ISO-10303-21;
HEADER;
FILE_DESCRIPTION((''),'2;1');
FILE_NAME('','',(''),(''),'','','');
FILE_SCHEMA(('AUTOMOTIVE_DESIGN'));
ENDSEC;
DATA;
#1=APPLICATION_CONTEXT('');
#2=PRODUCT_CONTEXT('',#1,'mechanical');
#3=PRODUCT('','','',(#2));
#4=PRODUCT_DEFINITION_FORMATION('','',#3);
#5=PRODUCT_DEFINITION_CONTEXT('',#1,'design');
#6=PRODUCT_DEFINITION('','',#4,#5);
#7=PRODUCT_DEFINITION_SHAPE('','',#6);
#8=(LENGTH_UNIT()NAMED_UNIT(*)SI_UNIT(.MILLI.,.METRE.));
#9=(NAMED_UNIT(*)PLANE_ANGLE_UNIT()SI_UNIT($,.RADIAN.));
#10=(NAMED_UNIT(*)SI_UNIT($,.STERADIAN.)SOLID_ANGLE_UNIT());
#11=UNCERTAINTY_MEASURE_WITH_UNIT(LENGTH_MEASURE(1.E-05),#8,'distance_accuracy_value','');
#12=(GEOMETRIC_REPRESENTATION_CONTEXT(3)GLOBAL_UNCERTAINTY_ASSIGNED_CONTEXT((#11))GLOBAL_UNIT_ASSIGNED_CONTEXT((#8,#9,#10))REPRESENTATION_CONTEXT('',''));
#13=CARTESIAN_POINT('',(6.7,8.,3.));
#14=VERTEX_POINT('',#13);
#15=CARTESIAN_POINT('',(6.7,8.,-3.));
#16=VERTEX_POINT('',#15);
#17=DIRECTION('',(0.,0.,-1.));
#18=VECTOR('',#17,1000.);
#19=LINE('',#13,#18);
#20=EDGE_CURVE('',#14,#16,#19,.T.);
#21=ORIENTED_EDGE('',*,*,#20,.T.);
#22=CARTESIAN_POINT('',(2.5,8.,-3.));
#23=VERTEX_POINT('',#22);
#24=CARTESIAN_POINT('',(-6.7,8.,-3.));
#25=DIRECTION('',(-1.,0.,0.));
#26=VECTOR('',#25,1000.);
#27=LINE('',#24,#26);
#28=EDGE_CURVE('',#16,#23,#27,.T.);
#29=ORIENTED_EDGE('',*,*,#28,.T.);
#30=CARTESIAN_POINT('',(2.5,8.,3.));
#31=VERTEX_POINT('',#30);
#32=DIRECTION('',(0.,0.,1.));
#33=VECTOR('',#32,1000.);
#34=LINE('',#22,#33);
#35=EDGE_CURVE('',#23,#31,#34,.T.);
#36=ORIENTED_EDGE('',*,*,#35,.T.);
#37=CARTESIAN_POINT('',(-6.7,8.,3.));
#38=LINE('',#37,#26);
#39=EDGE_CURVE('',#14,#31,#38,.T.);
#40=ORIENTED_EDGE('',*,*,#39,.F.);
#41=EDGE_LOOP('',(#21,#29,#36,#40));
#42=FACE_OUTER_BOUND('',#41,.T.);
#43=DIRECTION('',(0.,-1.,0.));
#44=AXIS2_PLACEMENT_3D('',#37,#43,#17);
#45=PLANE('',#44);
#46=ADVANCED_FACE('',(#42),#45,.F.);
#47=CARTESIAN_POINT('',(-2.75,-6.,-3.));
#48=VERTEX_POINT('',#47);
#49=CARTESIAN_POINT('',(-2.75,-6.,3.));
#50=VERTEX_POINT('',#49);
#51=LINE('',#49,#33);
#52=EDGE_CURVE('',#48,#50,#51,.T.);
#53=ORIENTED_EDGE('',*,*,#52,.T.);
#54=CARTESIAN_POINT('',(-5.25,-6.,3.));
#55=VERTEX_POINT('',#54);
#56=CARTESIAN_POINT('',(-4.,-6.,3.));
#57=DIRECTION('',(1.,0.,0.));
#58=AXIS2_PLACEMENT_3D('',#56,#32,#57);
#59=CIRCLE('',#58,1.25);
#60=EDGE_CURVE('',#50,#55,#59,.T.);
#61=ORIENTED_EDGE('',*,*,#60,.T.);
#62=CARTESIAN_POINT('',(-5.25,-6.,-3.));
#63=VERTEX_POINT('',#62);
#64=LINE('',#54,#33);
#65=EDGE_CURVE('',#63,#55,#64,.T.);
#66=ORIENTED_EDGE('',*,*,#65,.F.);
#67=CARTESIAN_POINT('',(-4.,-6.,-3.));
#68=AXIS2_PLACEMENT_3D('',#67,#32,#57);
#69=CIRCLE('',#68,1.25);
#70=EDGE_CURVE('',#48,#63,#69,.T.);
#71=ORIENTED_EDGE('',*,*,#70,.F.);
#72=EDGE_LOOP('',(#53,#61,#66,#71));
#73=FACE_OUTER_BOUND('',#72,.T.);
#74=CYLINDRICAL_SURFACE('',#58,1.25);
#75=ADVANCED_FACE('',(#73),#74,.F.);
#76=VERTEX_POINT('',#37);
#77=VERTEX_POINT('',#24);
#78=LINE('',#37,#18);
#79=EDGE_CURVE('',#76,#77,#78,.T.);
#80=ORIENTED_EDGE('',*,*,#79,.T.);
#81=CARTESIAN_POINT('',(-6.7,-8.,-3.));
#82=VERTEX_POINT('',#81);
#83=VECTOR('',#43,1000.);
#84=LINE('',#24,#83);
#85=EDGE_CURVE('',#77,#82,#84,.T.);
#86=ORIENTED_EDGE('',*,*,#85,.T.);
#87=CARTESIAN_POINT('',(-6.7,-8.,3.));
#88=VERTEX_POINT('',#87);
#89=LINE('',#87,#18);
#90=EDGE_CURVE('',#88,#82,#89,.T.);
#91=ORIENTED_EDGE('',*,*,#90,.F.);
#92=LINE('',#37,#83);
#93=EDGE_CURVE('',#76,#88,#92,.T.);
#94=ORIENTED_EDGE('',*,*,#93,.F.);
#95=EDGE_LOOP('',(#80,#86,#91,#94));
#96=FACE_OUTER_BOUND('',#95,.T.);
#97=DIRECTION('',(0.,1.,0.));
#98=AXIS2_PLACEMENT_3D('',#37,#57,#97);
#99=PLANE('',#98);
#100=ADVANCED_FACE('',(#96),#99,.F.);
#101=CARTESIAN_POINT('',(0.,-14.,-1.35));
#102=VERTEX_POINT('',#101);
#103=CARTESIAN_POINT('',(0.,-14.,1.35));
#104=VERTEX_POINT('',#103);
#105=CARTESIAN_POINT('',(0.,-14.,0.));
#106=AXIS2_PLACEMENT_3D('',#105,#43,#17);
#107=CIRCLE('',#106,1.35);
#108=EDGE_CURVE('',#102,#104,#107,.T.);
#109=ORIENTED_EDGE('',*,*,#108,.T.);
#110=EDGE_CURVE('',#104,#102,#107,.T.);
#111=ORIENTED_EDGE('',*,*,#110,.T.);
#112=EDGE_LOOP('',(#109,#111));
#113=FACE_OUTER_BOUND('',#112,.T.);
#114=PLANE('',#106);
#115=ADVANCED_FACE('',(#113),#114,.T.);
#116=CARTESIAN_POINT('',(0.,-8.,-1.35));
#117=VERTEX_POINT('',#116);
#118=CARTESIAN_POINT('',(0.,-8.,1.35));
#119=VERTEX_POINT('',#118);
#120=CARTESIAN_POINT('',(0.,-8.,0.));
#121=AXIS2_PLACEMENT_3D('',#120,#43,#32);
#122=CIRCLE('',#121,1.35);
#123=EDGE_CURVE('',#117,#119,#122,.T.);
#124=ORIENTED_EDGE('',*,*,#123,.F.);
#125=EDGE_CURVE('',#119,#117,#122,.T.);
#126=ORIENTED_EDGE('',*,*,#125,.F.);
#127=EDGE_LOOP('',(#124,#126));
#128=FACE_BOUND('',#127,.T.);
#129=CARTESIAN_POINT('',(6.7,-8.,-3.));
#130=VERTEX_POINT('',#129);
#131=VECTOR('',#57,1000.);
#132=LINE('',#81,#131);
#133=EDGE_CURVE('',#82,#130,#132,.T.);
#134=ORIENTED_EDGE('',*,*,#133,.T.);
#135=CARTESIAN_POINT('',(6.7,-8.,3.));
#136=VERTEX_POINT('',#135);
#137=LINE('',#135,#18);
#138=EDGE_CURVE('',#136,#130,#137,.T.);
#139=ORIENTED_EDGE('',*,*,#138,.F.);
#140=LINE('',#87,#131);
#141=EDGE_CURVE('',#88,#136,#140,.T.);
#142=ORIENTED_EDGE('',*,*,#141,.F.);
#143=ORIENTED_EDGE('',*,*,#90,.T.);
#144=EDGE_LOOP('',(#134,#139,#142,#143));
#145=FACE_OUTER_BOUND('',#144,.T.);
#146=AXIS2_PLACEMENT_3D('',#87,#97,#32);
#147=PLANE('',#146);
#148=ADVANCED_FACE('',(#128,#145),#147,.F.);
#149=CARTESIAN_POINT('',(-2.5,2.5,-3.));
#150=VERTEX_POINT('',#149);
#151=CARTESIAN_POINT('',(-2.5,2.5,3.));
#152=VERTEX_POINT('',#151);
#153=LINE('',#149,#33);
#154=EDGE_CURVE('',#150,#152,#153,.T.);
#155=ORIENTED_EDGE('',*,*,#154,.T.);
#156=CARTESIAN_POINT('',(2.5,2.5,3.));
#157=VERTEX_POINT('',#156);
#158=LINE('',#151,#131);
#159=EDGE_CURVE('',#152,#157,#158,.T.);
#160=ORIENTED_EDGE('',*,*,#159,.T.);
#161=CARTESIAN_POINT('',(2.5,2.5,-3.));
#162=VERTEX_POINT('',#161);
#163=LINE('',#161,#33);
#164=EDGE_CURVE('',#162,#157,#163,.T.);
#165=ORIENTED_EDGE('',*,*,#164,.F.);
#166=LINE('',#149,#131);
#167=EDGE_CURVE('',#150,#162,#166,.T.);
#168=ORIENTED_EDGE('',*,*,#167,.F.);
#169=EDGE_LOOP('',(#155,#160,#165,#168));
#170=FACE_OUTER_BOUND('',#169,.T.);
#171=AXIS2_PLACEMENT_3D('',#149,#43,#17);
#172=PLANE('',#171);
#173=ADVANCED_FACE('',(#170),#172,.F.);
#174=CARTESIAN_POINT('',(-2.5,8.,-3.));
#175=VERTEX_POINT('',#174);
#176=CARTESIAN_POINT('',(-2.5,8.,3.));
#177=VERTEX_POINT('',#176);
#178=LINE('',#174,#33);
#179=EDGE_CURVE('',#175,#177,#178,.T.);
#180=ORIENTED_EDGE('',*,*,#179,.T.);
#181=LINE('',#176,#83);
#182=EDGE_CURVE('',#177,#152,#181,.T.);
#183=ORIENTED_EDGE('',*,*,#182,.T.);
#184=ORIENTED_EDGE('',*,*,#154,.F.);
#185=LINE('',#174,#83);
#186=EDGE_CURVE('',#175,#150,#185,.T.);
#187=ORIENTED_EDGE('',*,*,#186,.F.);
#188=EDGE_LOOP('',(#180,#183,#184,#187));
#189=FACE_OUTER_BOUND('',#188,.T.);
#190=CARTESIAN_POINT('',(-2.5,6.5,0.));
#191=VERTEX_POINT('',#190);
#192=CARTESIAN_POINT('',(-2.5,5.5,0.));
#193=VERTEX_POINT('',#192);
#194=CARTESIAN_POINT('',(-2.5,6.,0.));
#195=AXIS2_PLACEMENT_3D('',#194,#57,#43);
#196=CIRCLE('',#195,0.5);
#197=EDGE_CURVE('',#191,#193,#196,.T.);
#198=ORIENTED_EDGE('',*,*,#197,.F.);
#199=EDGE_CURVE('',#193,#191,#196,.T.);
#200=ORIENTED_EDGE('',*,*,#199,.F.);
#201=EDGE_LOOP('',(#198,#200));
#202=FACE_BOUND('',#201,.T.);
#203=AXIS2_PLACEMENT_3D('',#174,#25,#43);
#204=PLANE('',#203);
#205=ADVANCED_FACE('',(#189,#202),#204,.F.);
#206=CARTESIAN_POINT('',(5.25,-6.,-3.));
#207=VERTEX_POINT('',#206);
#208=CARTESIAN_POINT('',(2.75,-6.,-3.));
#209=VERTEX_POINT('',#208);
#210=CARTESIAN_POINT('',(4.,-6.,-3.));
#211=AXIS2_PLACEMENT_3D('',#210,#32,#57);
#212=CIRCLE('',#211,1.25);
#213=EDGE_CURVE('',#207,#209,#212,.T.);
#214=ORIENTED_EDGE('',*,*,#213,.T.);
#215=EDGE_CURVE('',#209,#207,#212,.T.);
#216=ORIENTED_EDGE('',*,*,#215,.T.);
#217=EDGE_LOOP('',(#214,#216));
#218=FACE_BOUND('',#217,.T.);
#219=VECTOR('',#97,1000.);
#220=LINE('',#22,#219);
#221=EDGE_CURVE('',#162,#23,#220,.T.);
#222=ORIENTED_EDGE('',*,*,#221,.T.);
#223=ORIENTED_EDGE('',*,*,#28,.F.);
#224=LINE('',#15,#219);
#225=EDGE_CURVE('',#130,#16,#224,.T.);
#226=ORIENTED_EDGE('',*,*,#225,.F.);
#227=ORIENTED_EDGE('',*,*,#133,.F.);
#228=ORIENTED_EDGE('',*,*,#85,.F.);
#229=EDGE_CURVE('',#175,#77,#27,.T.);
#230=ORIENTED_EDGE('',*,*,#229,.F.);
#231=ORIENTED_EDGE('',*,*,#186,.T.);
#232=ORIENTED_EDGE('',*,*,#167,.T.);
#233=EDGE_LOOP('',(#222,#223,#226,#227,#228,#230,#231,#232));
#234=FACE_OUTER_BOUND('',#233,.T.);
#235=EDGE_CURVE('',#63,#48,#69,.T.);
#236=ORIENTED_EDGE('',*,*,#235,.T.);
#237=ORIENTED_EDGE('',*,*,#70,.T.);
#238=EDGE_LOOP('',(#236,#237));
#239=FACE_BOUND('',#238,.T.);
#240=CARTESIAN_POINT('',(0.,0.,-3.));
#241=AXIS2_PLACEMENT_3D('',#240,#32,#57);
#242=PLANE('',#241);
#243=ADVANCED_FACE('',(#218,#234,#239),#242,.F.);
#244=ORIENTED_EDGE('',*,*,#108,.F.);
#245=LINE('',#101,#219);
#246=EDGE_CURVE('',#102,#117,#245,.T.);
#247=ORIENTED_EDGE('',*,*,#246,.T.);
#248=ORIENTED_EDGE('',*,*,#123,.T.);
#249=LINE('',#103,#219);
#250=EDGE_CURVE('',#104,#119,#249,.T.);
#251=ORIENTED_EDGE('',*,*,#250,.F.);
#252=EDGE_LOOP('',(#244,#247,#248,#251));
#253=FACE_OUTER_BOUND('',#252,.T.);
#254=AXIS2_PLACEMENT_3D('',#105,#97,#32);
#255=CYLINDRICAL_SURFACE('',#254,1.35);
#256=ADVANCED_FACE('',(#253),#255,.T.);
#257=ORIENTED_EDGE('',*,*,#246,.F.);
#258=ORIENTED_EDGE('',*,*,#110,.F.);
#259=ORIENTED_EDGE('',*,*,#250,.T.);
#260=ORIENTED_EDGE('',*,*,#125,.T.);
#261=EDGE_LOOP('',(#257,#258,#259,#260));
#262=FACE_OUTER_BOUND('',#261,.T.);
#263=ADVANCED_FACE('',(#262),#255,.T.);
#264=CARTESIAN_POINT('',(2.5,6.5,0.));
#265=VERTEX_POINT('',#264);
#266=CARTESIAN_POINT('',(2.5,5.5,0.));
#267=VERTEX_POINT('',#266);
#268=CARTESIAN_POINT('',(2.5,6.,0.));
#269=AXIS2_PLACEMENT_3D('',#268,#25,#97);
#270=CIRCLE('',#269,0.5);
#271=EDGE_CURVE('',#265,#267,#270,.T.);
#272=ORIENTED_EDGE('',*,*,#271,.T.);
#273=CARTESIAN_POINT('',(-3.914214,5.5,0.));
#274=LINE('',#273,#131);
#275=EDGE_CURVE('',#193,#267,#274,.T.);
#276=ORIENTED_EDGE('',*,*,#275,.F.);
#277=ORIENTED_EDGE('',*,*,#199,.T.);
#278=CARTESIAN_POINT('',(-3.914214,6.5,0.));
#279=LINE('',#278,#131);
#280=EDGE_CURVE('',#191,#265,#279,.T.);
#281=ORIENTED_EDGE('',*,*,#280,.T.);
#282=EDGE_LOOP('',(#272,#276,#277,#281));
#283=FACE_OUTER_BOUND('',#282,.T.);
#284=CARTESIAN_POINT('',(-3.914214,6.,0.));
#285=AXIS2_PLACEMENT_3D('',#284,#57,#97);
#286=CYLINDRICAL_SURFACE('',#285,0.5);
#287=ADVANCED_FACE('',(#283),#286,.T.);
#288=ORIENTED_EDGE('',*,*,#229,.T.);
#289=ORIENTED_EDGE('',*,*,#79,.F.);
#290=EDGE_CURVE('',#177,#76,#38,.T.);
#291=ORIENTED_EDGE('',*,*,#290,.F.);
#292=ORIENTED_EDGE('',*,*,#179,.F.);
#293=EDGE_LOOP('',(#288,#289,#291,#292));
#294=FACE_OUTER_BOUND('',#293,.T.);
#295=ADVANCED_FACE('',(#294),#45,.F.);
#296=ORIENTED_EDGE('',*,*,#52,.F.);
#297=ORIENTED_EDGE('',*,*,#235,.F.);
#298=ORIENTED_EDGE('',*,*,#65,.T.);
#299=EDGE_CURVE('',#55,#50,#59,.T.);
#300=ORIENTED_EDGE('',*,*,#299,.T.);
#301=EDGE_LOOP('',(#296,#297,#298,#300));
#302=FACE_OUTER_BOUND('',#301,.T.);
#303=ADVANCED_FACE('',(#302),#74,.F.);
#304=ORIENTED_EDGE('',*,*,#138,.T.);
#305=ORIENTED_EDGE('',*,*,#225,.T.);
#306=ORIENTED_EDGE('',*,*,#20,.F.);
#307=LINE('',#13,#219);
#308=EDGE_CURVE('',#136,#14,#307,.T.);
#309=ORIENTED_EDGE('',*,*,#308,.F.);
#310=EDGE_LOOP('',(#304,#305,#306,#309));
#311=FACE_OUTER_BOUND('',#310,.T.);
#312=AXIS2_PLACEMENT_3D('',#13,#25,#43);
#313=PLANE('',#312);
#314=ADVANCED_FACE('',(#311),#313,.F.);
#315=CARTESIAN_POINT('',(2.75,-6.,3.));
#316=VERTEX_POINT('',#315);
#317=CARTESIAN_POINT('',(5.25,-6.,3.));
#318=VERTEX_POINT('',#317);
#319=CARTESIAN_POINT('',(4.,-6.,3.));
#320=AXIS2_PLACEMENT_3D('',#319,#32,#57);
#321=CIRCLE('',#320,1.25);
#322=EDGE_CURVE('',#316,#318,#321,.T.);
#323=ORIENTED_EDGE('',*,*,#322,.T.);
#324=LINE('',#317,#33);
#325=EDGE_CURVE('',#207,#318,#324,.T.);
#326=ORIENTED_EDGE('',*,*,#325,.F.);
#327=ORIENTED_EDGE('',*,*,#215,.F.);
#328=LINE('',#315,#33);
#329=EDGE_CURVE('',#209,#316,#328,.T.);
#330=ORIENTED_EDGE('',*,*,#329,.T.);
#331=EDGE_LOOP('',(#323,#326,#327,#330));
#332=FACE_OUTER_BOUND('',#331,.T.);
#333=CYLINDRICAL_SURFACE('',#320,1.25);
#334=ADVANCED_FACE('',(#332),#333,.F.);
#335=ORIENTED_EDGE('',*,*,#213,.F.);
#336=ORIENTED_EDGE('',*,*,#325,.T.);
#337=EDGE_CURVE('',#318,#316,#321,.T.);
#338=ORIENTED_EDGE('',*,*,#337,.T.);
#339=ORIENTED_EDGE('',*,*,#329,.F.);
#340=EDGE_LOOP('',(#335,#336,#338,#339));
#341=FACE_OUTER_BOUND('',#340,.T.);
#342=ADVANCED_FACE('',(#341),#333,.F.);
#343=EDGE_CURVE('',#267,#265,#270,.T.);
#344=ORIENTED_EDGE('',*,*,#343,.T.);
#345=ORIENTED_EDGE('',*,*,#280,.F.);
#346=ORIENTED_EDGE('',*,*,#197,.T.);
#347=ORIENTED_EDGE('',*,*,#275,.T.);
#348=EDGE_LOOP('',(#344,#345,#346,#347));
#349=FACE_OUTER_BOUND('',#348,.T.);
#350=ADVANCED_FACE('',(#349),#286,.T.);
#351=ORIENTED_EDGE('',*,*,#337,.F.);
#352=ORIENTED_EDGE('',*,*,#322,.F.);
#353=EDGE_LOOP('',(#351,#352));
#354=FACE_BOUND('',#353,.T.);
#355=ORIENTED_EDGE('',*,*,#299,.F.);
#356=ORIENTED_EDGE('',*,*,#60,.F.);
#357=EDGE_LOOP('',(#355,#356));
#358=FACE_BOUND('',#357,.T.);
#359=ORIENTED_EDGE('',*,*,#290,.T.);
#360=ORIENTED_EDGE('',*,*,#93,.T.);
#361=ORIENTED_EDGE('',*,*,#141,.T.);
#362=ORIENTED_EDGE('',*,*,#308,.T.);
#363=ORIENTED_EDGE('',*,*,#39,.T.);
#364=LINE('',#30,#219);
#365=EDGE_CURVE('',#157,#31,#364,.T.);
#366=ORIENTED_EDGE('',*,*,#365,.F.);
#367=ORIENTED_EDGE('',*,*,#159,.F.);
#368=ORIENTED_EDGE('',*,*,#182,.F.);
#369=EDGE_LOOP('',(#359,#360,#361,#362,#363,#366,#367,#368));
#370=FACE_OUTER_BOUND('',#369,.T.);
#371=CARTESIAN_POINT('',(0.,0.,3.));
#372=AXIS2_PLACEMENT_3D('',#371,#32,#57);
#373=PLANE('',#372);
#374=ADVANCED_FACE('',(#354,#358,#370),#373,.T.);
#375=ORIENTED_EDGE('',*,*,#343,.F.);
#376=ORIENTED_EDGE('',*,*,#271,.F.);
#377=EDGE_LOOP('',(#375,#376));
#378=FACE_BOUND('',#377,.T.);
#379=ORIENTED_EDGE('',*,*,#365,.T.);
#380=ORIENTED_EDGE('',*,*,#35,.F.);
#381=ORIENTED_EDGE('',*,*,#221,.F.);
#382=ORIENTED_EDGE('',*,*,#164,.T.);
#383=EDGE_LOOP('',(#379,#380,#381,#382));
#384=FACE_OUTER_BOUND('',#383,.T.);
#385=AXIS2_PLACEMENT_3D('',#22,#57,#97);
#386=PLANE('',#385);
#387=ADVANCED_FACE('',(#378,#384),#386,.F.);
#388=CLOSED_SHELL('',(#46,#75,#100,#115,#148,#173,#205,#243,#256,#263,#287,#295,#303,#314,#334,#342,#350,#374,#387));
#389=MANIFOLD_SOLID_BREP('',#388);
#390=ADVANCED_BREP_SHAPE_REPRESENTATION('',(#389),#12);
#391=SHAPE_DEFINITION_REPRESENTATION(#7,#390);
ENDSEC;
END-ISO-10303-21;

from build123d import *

# Parameters (mm, degrees)
SKETCH1_W                  = 13.4
SKETCH1_H                  = 16
BOSS_EXTRUDE1_DEPTH        = 3
SKETCH2_W                  = 5
SKETCH2_H                  = 5.5
CUT_EXTRUDE1_DEPTH         = 13.037026211
SKETCH3_R                  = 1.35
BOSS_EXTRUDE2_DEPTH        = 6
F_2_5_2_5_DIAMETER_HOLE1_D = 2.5
SKETCH6_R                  = 0.5
BOSS_EXTRUDE3_DEPTH        = 5


with BuildPart() as part:
    # Sketch1 → Boss-Extrude1 (new, symmetric)
    with BuildSketch(Plane.XY):
        Rectangle(SKETCH1_W, SKETCH1_H)
    extrude(amount=BOSS_EXTRUDE1_DEPTH, both=True)

    # Sketch2 → Cut-Extrude1 (cut, through all)
    with BuildSketch(Plane.XY.offset(3)):
        with Locations((0, 5.25)):
            Rectangle(SKETCH2_W, SKETCH2_H)
    extrude(amount=-CUT_EXTRUDE1_DEPTH, mode=Mode.SUBTRACT)

    # Sketch3 → Boss-Extrude2 (add)
    with BuildSketch(Plane.XZ.offset(8)):
        with Locations(Location((0, 0, 0), (0, 0, 90))):
            Circle(SKETCH3_R)
    extrude(amount=BOSS_EXTRUDE2_DEPTH)

    # Ø2.5 (2.5) Diameter Hole1 (through all)
    with Locations(Plane.XY.offset(3)):
        with Locations((-4, -6), (4, -6)):
            Hole(F_2_5_2_5_DIAMETER_HOLE1_D / 2)

    # Sketch6 → Boss-Extrude3 (add)
    with BuildSketch(Plane.ZY.offset(-2.5)):
        with Locations(Location((0, 6, 0), (0, 0, 90))):
            Circle(SKETCH6_R)
    extrude(amount=BOSS_EXTRUDE3_DEPTH)


solid = part.part
